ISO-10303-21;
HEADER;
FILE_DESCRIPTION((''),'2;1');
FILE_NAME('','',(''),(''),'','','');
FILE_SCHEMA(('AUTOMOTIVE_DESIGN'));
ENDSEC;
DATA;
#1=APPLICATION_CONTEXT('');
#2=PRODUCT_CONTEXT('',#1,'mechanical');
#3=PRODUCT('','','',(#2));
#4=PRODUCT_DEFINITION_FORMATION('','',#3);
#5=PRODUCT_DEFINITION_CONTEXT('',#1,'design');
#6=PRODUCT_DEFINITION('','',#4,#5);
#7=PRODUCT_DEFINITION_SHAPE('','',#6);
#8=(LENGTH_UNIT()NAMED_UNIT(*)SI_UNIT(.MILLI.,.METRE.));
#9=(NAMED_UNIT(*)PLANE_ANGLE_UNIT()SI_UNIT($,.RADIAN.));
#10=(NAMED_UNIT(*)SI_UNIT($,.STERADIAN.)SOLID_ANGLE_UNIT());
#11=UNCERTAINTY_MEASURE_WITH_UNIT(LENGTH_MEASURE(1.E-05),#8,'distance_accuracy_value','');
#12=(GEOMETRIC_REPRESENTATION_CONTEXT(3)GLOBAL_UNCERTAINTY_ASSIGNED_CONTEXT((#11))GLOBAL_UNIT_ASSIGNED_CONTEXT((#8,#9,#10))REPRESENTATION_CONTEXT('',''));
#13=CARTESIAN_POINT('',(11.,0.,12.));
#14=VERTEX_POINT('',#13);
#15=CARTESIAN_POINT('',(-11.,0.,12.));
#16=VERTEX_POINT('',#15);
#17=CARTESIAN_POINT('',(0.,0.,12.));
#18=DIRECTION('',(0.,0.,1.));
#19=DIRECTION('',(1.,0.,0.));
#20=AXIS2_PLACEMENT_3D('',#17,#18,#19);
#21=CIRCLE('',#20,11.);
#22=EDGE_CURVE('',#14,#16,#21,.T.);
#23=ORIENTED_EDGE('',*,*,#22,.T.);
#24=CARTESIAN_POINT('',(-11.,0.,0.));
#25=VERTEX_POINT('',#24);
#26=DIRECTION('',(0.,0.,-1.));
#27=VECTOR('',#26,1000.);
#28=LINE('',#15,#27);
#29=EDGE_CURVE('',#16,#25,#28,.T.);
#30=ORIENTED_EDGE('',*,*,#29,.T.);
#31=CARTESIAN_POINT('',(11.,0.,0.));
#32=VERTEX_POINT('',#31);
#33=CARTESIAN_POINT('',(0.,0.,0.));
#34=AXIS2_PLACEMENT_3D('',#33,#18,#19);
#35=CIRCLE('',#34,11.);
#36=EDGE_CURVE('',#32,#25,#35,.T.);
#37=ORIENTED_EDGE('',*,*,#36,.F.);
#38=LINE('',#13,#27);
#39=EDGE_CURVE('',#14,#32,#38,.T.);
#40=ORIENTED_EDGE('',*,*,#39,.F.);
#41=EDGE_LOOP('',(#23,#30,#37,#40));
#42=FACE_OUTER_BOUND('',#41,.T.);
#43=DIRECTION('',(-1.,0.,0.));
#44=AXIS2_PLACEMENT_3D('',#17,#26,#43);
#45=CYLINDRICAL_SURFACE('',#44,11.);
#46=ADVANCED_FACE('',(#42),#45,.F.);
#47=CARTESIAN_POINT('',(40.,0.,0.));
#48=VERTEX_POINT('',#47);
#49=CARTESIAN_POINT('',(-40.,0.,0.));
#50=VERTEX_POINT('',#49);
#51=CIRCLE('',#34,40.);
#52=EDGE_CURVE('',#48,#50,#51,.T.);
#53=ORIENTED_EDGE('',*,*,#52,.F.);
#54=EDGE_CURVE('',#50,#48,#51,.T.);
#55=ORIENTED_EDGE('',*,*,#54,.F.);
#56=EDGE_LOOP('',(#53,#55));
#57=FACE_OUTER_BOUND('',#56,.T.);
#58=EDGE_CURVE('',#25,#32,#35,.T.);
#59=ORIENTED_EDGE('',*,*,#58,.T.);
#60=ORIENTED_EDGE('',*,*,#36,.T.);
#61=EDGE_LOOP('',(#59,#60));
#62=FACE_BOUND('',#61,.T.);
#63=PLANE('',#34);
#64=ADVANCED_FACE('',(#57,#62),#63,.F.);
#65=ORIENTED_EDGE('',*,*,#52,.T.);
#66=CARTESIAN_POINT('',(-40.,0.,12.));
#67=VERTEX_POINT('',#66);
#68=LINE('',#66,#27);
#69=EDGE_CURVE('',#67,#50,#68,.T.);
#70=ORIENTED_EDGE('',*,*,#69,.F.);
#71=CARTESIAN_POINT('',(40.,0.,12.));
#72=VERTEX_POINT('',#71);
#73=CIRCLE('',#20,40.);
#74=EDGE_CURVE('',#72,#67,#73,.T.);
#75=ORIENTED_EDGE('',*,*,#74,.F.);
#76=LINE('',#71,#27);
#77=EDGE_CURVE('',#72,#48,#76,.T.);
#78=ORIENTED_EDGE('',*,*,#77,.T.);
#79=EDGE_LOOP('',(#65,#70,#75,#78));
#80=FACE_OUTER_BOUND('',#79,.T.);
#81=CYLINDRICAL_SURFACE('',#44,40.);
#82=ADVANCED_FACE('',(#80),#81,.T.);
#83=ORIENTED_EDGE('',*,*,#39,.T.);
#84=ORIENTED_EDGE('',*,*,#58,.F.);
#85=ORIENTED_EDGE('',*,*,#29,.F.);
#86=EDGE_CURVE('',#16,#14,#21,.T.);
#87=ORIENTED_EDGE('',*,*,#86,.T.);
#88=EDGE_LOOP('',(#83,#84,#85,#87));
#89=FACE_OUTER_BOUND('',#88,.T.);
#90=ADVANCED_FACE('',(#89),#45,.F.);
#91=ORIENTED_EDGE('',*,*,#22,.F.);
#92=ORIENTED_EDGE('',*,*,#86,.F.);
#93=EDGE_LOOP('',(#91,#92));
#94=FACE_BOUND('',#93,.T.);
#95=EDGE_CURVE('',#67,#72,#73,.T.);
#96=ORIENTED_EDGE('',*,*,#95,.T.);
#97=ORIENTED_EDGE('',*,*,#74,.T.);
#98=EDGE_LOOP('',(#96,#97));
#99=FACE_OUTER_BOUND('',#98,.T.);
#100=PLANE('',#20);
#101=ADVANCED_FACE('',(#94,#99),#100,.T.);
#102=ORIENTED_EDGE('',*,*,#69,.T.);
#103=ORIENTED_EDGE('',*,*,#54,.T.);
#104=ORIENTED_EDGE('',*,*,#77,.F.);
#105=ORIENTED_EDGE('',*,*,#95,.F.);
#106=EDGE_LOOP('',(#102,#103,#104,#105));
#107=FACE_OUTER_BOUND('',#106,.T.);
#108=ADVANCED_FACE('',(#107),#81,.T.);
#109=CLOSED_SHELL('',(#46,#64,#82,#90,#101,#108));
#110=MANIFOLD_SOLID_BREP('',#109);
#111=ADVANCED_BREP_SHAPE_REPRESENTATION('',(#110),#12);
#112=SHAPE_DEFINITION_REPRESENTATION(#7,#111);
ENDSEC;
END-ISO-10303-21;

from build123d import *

# Parameters (mm, degrees)
SKETCH1_R           = 40
SKETCH1_R_2         = 11
BOSS_EXTRUDE1_DEPTH = 12


with BuildPart() as part:
    # Sketch1 → Boss-Extrude1 (new body)
    with BuildSketch(Plane.XY):
        Circle(SKETCH1_R)
        Circle(SKETCH1_R_2, mode=Mode.SUBTRACT)
    extrude(amount=BOSS_EXTRUDE1_DEPTH)


solid = part.part
